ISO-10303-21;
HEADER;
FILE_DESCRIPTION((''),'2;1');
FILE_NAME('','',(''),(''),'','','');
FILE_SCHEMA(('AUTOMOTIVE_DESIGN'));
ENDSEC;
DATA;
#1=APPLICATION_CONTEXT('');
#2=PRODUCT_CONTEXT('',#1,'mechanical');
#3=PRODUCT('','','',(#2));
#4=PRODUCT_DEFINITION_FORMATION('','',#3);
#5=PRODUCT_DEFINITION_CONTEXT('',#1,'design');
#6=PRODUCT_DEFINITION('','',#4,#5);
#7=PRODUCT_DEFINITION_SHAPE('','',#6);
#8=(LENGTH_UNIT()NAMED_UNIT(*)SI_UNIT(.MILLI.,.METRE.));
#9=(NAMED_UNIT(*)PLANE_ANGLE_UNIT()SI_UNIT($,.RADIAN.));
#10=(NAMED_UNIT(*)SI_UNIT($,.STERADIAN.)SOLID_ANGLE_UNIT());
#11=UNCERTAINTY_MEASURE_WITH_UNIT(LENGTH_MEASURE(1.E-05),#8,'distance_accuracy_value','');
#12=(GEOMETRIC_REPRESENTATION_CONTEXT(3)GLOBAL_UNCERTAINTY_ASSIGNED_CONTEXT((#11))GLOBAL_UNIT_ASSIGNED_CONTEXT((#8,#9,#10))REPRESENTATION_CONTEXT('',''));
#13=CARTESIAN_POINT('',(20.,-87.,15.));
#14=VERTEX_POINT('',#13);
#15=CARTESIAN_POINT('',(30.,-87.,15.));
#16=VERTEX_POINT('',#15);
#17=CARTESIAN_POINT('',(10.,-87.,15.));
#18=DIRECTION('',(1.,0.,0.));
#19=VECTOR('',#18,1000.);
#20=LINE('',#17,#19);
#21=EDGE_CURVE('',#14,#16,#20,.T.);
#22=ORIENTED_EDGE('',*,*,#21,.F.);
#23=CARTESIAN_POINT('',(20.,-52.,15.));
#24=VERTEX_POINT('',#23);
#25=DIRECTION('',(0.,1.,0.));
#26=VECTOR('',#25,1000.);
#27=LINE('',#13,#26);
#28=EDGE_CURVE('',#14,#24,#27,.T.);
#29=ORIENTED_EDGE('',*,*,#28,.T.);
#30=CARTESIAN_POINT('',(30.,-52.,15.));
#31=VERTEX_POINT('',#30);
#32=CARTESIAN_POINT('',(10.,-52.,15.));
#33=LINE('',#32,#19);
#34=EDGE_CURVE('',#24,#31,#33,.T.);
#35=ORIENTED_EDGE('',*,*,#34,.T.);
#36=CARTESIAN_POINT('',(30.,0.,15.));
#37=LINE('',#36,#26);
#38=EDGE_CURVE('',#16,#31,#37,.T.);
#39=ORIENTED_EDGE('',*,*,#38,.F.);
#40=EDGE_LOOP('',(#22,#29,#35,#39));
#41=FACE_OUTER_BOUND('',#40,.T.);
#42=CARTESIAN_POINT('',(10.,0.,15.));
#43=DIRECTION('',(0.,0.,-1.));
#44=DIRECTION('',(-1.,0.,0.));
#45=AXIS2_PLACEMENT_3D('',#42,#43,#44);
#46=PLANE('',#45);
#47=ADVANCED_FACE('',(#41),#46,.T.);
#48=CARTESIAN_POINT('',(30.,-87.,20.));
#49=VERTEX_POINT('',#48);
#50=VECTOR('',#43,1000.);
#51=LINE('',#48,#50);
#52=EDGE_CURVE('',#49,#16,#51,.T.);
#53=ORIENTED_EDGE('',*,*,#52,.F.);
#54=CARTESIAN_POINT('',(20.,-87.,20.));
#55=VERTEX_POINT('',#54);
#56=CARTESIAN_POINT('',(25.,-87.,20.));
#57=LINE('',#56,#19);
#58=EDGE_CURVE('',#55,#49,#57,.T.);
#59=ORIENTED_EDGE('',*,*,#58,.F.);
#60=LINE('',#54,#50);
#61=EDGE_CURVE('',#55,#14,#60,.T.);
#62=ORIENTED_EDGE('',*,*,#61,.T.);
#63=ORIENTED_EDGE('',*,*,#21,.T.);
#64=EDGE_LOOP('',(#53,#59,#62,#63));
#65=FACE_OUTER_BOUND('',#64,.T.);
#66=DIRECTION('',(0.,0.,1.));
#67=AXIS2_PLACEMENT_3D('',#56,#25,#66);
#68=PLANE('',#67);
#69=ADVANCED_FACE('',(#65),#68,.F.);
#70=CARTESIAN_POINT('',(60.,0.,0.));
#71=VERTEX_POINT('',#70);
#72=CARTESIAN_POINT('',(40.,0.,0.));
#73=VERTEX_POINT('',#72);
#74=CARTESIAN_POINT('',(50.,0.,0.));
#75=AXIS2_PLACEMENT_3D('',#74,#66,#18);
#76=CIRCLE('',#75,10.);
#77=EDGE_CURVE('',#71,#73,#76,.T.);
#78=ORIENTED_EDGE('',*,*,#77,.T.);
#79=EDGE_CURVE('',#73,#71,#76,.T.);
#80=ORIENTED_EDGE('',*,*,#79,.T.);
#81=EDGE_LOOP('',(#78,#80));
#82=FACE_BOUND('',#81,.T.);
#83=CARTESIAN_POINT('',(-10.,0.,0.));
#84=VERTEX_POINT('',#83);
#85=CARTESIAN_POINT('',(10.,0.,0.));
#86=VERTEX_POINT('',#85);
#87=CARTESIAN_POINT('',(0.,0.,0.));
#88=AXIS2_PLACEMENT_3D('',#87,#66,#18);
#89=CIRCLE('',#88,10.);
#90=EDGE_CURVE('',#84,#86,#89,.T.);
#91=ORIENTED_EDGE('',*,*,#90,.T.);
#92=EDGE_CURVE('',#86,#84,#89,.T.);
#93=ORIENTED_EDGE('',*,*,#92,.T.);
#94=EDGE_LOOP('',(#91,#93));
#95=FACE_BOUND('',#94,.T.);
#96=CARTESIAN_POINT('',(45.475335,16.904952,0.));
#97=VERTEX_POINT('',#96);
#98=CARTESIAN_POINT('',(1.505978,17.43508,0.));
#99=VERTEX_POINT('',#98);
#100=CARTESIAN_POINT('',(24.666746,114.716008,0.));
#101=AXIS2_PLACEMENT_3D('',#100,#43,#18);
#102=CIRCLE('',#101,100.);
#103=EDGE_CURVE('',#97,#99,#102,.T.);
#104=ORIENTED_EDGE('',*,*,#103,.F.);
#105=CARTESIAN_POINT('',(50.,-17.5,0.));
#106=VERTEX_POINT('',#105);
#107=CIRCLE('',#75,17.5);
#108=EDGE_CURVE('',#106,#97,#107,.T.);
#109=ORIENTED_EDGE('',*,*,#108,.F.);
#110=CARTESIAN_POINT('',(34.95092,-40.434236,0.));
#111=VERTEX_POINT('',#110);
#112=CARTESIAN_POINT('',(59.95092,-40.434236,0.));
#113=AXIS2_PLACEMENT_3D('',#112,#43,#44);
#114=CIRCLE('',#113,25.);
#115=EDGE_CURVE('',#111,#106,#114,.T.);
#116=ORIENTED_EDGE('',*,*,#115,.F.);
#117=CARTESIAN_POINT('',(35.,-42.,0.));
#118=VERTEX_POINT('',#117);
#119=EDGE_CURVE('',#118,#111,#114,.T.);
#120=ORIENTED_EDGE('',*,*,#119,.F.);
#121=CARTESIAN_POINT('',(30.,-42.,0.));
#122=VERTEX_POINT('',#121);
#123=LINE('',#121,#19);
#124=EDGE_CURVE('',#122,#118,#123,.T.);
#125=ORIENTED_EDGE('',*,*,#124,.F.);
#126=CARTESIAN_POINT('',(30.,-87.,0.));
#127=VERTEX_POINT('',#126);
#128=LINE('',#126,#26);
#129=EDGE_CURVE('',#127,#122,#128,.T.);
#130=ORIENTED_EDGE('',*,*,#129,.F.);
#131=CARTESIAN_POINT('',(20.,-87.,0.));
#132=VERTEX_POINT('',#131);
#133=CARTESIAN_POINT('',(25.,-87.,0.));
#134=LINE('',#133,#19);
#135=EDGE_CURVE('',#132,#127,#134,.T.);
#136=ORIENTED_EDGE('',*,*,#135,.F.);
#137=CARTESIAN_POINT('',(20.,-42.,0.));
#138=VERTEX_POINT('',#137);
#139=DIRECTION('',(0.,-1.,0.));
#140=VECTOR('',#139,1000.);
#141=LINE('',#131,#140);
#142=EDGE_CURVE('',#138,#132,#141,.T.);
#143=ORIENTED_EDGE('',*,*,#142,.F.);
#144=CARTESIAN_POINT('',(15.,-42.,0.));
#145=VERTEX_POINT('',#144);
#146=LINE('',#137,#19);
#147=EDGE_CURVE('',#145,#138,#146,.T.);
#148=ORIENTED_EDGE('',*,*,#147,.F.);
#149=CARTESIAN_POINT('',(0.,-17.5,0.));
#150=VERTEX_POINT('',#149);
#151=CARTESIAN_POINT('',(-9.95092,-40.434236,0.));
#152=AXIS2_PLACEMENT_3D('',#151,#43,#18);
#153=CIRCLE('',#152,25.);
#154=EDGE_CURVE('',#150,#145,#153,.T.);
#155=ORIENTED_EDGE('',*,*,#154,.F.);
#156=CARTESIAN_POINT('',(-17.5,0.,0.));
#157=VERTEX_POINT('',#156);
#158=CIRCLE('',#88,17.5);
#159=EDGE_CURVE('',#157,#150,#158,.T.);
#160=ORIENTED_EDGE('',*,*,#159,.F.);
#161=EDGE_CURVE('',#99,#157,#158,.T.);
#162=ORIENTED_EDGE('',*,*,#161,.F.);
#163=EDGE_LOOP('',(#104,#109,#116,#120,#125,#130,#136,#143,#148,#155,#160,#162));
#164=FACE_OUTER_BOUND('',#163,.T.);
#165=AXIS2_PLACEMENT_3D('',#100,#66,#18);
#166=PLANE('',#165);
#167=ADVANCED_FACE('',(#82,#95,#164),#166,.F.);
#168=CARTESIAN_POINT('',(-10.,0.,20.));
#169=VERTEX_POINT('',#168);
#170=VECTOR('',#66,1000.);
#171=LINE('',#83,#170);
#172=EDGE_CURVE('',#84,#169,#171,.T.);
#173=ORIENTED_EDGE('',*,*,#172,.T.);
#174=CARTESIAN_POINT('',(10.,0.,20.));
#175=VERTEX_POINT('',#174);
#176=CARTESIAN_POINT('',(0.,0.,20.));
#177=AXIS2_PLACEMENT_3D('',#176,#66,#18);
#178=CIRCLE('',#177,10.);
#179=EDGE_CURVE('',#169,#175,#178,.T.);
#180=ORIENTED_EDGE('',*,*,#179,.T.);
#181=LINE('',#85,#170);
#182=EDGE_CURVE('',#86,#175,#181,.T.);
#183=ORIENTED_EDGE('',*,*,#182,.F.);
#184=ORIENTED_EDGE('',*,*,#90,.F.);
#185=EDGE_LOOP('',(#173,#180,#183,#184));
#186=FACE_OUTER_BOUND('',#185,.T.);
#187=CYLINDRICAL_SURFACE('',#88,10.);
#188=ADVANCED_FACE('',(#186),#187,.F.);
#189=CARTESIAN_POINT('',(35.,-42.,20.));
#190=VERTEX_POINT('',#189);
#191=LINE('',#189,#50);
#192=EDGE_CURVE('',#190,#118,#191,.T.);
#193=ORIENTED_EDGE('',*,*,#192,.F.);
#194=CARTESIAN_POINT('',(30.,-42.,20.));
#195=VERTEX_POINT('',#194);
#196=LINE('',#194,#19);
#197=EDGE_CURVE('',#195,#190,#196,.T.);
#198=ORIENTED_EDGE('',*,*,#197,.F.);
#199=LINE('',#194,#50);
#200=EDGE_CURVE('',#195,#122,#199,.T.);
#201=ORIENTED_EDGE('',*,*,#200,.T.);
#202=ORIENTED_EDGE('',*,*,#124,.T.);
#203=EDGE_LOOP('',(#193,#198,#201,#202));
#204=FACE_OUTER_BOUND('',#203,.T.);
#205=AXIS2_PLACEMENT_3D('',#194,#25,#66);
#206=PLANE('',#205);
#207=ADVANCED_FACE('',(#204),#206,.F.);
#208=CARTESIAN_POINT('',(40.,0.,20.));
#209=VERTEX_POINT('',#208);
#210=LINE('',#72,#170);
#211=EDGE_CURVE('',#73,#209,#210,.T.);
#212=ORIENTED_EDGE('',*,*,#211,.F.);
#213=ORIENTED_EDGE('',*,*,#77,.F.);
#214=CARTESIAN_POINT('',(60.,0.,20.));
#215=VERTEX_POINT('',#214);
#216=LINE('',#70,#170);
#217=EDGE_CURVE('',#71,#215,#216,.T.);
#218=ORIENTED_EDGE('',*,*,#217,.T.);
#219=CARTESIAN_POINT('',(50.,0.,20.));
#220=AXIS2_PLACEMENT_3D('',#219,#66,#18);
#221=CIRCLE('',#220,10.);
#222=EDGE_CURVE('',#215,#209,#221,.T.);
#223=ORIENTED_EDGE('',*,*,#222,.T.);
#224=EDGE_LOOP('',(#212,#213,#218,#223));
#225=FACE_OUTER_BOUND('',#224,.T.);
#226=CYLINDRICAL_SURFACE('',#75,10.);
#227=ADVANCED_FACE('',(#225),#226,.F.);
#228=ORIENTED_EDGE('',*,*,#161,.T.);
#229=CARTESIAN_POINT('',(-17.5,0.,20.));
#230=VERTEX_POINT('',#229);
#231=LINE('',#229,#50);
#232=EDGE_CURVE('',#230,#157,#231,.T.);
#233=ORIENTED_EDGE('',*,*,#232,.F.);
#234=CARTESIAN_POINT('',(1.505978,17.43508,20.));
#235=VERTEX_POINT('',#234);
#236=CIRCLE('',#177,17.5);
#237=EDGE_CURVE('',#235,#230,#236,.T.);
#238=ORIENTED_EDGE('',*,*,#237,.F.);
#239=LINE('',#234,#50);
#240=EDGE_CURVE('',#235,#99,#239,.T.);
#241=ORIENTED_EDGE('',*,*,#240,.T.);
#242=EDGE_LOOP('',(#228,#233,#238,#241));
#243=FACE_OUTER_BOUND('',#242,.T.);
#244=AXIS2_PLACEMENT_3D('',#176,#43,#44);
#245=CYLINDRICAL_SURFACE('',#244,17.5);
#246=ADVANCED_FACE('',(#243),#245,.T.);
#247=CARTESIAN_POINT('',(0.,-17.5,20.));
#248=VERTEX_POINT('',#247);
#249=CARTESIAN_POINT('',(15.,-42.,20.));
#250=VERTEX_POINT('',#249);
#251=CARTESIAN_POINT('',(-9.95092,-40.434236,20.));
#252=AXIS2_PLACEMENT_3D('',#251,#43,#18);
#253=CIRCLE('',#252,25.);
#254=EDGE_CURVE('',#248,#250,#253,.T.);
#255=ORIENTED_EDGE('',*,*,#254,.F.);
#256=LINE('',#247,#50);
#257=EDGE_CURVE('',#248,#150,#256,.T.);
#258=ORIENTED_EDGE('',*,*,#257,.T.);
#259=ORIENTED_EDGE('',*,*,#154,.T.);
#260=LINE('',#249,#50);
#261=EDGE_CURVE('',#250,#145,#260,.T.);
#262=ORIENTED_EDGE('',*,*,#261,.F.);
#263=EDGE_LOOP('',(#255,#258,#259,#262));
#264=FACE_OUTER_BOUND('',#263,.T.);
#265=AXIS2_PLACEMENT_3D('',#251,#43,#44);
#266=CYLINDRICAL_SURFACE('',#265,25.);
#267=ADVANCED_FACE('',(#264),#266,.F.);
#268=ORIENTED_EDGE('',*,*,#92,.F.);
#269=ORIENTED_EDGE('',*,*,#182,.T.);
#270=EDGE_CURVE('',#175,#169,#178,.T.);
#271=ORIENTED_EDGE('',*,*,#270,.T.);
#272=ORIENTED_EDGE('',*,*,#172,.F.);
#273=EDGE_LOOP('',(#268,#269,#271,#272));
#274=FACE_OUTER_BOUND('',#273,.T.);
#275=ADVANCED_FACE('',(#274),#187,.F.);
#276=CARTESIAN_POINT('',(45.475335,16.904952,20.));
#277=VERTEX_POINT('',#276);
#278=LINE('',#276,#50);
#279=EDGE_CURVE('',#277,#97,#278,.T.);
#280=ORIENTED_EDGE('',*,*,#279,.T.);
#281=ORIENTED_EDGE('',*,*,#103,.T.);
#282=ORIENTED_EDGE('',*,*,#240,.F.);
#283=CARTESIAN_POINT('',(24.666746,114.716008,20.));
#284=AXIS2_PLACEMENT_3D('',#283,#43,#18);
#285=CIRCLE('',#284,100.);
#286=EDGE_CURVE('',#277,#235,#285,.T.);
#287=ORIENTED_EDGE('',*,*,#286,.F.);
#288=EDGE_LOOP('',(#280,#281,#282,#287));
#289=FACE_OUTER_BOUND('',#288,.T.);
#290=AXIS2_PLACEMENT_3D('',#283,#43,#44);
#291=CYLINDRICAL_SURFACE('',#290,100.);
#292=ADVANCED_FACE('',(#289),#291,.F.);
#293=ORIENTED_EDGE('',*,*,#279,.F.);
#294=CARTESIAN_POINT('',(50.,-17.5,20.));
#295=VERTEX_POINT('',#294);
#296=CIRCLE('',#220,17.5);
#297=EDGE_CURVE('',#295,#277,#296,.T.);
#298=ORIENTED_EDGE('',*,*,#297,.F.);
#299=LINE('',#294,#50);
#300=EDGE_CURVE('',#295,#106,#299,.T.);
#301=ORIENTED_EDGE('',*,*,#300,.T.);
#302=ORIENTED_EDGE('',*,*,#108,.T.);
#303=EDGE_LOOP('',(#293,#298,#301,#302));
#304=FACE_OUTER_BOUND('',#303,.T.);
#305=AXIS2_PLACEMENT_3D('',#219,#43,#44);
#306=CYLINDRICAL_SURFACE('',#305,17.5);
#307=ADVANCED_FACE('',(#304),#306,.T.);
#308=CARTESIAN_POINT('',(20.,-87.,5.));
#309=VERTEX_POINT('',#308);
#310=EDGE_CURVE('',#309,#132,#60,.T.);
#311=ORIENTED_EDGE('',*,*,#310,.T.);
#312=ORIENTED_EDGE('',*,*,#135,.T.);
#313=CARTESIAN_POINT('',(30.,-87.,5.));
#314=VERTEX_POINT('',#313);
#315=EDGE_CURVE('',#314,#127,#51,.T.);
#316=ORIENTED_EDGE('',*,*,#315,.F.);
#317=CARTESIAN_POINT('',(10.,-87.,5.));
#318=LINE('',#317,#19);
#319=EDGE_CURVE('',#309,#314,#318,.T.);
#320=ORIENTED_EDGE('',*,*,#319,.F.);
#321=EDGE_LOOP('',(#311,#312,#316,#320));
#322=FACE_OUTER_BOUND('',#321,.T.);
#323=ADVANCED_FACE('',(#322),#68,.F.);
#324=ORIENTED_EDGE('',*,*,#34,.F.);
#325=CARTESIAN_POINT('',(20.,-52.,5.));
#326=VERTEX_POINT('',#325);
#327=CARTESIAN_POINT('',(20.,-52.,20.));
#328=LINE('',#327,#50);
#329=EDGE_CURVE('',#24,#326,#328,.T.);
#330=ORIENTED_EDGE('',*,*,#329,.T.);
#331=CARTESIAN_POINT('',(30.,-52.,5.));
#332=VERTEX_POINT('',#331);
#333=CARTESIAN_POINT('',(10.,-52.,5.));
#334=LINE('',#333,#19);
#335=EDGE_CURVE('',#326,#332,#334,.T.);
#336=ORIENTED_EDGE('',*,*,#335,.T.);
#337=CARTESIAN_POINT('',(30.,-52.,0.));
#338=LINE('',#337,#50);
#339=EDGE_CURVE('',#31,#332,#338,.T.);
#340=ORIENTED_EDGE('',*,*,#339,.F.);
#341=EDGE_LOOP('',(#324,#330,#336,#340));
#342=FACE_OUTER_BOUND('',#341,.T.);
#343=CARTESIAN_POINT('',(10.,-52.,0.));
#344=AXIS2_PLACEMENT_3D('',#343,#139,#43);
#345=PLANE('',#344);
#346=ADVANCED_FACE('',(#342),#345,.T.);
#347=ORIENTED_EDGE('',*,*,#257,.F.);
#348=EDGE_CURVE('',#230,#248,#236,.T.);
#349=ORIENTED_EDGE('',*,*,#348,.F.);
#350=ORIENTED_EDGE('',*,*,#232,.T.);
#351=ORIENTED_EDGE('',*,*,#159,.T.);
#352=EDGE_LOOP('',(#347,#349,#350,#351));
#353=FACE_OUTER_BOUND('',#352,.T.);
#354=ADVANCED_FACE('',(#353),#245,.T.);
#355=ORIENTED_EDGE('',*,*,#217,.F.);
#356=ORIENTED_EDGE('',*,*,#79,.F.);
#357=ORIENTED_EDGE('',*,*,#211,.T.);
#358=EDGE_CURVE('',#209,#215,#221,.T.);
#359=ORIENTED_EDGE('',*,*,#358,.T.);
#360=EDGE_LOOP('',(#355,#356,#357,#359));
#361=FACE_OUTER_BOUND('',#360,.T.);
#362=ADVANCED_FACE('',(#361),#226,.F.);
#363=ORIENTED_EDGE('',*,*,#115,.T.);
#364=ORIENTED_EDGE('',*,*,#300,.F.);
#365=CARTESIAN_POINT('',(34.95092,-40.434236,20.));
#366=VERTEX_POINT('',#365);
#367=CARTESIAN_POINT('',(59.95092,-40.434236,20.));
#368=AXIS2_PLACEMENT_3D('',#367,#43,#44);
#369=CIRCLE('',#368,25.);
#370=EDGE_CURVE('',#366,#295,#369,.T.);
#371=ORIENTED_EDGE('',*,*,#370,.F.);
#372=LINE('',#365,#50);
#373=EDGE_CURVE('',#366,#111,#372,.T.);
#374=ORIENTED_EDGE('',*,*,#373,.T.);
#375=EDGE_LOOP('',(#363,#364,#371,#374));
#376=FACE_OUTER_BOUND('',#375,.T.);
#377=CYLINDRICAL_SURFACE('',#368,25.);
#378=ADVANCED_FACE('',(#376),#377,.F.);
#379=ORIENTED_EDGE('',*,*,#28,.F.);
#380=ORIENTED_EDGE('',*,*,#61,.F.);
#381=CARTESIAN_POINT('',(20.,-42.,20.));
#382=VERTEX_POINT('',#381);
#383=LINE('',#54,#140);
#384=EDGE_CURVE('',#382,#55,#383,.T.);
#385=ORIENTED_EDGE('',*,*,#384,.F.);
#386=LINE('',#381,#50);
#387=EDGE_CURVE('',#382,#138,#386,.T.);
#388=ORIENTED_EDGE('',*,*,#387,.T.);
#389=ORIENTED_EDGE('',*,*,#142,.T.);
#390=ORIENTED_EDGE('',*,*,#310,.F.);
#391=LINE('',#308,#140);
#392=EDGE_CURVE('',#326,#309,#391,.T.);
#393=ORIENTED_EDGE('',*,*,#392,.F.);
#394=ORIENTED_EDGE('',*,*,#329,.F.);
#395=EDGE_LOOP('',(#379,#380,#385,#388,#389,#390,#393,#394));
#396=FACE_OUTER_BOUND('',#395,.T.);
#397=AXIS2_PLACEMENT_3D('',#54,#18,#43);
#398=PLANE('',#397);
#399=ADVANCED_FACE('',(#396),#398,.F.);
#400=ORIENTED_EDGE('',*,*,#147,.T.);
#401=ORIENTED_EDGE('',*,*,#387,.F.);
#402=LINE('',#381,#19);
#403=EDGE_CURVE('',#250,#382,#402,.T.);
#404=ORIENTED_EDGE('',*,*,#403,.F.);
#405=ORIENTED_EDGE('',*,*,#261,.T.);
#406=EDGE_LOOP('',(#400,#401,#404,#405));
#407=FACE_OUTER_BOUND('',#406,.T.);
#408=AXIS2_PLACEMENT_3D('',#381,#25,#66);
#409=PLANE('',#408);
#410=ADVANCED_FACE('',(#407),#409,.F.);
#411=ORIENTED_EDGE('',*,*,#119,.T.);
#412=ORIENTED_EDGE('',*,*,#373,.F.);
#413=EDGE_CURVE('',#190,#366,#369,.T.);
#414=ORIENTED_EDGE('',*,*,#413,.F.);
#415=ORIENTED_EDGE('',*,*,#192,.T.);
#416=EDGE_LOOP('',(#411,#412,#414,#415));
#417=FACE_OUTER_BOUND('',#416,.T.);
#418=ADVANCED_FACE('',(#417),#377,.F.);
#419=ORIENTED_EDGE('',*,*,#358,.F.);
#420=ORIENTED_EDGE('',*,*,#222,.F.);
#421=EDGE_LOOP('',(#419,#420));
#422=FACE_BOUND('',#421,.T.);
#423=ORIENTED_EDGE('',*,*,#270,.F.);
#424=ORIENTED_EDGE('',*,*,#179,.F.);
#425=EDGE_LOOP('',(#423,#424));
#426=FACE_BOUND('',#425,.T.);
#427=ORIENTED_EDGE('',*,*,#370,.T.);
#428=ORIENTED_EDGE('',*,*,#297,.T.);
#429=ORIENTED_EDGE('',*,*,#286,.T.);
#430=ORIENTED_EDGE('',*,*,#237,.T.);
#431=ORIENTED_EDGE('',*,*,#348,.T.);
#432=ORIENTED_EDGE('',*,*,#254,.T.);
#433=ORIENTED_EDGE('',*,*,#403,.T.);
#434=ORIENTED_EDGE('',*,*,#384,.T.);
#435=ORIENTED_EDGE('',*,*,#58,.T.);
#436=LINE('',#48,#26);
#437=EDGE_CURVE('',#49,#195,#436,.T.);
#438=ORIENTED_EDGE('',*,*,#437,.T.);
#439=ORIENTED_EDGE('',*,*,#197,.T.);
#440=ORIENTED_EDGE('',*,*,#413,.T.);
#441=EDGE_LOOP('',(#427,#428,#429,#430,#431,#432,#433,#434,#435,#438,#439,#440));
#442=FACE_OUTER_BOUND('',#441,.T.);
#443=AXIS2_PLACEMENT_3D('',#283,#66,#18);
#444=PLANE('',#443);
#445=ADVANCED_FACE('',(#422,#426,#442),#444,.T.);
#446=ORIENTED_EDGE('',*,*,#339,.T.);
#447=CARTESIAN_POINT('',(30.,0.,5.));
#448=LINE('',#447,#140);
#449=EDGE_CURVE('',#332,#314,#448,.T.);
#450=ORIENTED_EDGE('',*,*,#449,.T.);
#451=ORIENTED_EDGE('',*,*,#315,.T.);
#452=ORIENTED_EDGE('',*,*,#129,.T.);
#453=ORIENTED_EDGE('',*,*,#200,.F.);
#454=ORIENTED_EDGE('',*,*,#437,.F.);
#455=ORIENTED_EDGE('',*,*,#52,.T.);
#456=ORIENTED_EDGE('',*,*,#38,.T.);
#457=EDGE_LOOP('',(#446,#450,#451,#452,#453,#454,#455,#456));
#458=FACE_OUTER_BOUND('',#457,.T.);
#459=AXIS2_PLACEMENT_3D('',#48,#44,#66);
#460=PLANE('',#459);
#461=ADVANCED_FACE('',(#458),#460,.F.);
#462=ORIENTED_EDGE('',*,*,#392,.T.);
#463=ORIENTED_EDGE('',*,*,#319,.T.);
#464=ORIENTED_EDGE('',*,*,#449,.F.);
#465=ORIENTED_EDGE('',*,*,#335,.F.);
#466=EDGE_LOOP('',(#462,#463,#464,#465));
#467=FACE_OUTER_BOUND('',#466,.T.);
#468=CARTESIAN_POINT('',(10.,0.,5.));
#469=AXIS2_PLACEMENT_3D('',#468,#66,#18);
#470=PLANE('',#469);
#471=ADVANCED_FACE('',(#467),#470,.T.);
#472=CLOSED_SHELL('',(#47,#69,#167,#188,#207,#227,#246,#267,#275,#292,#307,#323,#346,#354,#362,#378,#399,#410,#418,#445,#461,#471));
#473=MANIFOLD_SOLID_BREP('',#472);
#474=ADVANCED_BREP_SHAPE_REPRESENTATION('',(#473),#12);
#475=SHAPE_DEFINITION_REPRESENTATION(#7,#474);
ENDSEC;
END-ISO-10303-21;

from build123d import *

# Parameters (mm, degrees)
KEY_BODY_DEPTH         = 20
SHANK_SLOT_SKETCH_W    = 10
SHANK_SLOT_SKETCH_H    = 35
SHANK_SLOT_DEPTH       = 20
GRIP_HOLES_SKETCH_R    = 10
GRIP_HOLES_2X_20_DEPTH = 20


with BuildPart() as part:
    # Key Profile Sketch → Key Body (new body)
    with BuildSketch(Plane.XY):
        with BuildLine():
            Line((25, -87), (30, -87))
            Line((30, -87), (30, -42))
            Line((30, -42), (35, -42))
            ThreePointArc((35, -42), (38.629636909, -27.380389945), (50, -17.5))
            ThreePointArc((50, -17.5), (67.350600333, 2.28181246), (45.475335312, 16.904952217))
            ThreePointArc((45.475335312, 16.904952217), (23.461156875, 14.723275331), (1.505978003, 17.435080449))
            ThreePointArc((1.505978003, 17.435080449), (-17.483762579, 0.753688313), (0, -17.5))
            ThreePointArc((0, -17.5), (11.370363091, -27.380389945), (15, -42))
            Line((15, -42), (20, -42))
            Line((20, -42), (20, -87))
            Line((20, -87), (25, -87))
        make_face()
    extrude(amount=KEY_BODY_DEPTH)

    # Shank Slot Sketch → Shank Slot (cut)
    with BuildSketch(Plane(origin=(30, 0, 0), x_dir=(0, 0, -1), z_dir=(1, 0, 0))):
        with Locations((-10, -69.5)):
            Rectangle(SHANK_SLOT_SKETCH_W, SHANK_SLOT_SKETCH_H)
    extrude(amount=-SHANK_SLOT_DEPTH, mode=Mode.SUBTRACT)

    # Grip Holes Sketch → Grip Holes 2xØ20 (cut)
    with BuildSketch(Plane.XY.offset(20)):
        Circle(GRIP_HOLES_SKETCH_R)
        with Locations((50, 0)):
            Circle(GRIP_HOLES_SKETCH_R)
    extrude(amount=-GRIP_HOLES_2X_20_DEPTH, mode=Mode.SUBTRACT)


solid = part.part
